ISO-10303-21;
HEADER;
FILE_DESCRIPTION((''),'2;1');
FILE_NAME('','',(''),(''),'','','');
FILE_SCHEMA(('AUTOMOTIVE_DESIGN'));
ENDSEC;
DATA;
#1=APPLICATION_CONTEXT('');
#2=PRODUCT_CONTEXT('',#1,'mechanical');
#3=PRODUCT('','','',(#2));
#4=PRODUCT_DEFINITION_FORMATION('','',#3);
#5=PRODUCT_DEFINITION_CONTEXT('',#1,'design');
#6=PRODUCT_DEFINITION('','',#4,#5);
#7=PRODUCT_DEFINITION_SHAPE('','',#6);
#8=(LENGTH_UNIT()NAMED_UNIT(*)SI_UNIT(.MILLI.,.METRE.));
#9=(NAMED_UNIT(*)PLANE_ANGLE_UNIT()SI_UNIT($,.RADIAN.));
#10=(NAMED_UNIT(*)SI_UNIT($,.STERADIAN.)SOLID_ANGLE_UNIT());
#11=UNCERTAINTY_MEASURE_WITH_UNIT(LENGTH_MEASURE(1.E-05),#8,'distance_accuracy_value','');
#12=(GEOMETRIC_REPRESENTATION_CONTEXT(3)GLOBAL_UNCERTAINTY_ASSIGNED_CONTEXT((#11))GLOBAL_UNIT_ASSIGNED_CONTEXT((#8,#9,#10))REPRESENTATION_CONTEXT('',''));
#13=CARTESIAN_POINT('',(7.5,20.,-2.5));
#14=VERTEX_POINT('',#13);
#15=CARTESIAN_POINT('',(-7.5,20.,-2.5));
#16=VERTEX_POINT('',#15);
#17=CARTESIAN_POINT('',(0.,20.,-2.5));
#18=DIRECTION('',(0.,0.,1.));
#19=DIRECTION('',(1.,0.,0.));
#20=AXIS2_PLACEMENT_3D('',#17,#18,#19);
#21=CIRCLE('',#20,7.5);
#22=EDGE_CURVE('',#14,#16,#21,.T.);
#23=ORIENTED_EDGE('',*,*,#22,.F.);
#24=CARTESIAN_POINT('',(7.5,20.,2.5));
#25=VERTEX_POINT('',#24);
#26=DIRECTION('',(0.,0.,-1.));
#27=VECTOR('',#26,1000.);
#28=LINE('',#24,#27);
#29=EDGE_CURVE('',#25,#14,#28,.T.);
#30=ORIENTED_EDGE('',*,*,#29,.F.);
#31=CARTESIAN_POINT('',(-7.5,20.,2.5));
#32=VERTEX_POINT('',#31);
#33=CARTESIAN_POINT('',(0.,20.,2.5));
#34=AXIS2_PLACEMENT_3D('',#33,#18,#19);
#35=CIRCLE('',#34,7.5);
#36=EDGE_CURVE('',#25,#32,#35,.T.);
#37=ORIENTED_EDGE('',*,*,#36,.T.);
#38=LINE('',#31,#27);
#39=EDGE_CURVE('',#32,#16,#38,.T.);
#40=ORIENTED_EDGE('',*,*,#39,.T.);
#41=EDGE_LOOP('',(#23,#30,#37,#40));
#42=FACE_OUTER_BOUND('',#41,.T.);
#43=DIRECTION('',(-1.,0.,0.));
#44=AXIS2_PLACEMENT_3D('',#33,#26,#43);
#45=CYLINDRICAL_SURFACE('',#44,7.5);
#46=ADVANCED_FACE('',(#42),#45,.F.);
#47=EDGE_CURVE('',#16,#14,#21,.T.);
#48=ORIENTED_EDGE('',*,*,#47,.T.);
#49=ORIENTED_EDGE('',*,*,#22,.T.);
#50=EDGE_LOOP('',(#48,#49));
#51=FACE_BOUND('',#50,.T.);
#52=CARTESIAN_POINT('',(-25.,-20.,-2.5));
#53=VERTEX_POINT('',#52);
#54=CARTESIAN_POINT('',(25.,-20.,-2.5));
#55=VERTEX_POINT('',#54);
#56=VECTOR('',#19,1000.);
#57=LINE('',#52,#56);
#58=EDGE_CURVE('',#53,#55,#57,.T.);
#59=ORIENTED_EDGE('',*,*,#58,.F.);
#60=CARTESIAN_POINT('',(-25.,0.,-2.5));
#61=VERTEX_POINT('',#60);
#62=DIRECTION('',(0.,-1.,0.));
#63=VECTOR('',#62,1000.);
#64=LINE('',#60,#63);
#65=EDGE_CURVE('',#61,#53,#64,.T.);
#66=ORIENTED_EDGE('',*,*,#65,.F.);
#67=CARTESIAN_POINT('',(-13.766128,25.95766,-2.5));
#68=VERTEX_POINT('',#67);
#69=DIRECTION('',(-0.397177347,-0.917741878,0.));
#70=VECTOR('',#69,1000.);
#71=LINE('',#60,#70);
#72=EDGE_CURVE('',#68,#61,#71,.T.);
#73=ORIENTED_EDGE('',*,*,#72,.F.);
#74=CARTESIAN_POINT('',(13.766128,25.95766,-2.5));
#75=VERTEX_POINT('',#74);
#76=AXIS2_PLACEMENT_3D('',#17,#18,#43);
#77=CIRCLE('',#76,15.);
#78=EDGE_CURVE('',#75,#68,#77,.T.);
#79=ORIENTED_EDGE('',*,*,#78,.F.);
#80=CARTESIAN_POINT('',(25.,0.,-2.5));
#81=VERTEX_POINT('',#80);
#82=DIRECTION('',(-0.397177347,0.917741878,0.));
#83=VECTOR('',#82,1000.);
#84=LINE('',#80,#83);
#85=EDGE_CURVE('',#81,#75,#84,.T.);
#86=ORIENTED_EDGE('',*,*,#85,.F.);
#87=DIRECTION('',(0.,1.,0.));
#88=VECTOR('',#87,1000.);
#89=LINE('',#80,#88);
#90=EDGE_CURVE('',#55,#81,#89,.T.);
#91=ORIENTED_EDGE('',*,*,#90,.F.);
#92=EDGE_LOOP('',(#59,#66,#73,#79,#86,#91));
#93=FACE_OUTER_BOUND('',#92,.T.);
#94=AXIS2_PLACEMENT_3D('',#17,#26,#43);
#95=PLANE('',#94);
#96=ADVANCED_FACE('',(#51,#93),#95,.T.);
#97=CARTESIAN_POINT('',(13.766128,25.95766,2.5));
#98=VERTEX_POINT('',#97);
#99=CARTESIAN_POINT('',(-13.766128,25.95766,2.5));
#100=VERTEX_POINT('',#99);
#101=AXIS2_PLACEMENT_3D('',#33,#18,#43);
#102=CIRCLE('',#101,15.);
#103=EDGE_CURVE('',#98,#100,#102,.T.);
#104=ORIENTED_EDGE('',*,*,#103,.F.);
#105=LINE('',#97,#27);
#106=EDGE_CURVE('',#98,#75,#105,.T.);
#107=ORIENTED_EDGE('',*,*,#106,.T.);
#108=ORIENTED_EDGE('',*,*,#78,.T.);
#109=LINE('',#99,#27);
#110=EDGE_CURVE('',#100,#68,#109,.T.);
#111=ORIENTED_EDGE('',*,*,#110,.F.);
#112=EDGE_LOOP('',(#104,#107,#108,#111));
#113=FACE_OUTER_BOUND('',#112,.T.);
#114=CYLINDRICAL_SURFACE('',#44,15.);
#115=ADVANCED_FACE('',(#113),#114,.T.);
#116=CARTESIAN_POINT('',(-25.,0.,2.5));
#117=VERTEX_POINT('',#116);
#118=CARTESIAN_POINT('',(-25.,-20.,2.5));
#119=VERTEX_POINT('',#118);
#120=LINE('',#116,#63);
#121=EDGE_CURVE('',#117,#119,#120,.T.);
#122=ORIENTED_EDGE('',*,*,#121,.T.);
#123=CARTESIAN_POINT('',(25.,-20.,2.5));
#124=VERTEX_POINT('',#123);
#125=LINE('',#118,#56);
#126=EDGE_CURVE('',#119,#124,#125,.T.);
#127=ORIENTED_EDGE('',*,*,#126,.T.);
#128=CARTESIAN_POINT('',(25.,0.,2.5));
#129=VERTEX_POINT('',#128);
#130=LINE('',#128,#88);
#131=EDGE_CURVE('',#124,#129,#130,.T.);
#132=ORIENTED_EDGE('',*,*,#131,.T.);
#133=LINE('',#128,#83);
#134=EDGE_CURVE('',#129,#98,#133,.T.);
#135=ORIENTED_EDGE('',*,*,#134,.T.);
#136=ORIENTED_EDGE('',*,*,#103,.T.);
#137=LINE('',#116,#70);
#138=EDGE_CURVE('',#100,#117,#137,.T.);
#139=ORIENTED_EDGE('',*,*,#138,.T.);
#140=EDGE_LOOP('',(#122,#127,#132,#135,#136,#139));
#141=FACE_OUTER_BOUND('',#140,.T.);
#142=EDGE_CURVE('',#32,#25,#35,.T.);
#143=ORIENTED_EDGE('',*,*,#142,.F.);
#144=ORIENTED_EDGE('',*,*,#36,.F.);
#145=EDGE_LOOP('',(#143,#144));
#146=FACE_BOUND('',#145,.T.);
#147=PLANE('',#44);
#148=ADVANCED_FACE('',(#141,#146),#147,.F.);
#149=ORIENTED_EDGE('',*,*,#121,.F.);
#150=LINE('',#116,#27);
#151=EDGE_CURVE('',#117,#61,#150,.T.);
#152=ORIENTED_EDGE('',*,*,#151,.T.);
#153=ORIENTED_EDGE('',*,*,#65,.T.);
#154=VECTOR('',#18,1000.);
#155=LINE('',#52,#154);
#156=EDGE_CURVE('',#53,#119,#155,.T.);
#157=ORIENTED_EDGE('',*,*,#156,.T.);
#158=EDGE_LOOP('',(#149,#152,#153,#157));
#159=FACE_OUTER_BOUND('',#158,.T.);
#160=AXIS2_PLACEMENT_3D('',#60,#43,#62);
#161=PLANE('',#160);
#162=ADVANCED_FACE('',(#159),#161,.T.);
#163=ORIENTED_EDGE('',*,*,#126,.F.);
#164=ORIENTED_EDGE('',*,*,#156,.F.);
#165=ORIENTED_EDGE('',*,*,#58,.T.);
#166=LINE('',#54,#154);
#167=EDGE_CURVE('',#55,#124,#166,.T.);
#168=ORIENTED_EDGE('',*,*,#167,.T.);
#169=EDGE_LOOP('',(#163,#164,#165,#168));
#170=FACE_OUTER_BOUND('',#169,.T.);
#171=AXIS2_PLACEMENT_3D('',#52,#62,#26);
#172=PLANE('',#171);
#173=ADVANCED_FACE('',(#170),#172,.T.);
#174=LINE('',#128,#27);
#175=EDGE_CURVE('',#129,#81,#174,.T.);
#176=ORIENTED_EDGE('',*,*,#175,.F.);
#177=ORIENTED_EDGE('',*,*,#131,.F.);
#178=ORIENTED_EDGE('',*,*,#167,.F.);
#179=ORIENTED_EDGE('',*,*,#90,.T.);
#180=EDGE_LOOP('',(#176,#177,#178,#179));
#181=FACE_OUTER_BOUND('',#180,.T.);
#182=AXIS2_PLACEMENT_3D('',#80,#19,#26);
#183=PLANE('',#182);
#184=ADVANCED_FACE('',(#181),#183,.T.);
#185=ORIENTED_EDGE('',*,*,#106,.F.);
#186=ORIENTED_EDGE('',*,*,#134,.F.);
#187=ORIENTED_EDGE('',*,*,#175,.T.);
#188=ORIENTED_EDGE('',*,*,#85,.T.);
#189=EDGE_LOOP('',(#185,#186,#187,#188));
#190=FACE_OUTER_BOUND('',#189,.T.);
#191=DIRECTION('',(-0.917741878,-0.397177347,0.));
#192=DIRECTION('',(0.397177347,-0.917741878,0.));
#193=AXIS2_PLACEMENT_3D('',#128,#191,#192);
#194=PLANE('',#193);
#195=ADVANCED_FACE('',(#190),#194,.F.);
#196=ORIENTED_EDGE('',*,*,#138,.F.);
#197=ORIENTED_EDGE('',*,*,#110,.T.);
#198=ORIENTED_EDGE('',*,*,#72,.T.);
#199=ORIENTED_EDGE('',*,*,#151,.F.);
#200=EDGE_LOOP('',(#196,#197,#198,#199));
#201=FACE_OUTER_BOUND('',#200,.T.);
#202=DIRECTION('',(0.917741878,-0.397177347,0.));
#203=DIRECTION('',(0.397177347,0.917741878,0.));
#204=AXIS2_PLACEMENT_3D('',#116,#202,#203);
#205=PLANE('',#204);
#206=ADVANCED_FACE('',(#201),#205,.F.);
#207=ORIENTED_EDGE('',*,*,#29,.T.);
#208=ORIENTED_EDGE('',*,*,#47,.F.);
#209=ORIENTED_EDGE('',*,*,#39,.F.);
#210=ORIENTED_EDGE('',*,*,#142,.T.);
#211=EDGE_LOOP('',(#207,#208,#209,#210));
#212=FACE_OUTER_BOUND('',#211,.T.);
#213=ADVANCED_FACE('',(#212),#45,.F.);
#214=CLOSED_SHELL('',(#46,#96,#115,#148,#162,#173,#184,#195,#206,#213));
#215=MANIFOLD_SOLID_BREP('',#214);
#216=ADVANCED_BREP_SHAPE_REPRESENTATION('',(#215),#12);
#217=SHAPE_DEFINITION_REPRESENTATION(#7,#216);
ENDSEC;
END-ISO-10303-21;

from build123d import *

# Parameters (mm, degrees)
SKETCH1_R           = 7.5
BOSS_EXTRUDE1_DEPTH = 2.5
SKETCH2_W           = 50
SKETCH2_H           = 20
BOSS_EXTRUDE2_DEPTH = 5


with BuildPart() as part:
    # Sketch1 → Boss-Extrude1 (new, symmetric)
    with BuildSketch(Plane.XY):
        with BuildLine():
            Line((25, 0), (-25, 0))
            Line((-25, 0), (-13.76612817, 25.957660212))
            ThreePointArc((-13.76612817, 25.957660212), (0, 35), (13.76612817, 25.957660212))
            Line((13.76612817, 25.957660212), (25, 0))
        make_face()
        with Locations((0, 20)):
            Circle(SKETCH1_R, mode=Mode.SUBTRACT)
    extrude(amount=BOSS_EXTRUDE1_DEPTH, both=True)

    # Sketch2 → Boss-Extrude2 (add)
    with BuildSketch(Plane.XY.offset(2.5)):
        with Locations((0, -10)):
            Rectangle(SKETCH2_W, SKETCH2_H)
    extrude(amount=-BOSS_EXTRUDE2_DEPTH)


solid = part.part
